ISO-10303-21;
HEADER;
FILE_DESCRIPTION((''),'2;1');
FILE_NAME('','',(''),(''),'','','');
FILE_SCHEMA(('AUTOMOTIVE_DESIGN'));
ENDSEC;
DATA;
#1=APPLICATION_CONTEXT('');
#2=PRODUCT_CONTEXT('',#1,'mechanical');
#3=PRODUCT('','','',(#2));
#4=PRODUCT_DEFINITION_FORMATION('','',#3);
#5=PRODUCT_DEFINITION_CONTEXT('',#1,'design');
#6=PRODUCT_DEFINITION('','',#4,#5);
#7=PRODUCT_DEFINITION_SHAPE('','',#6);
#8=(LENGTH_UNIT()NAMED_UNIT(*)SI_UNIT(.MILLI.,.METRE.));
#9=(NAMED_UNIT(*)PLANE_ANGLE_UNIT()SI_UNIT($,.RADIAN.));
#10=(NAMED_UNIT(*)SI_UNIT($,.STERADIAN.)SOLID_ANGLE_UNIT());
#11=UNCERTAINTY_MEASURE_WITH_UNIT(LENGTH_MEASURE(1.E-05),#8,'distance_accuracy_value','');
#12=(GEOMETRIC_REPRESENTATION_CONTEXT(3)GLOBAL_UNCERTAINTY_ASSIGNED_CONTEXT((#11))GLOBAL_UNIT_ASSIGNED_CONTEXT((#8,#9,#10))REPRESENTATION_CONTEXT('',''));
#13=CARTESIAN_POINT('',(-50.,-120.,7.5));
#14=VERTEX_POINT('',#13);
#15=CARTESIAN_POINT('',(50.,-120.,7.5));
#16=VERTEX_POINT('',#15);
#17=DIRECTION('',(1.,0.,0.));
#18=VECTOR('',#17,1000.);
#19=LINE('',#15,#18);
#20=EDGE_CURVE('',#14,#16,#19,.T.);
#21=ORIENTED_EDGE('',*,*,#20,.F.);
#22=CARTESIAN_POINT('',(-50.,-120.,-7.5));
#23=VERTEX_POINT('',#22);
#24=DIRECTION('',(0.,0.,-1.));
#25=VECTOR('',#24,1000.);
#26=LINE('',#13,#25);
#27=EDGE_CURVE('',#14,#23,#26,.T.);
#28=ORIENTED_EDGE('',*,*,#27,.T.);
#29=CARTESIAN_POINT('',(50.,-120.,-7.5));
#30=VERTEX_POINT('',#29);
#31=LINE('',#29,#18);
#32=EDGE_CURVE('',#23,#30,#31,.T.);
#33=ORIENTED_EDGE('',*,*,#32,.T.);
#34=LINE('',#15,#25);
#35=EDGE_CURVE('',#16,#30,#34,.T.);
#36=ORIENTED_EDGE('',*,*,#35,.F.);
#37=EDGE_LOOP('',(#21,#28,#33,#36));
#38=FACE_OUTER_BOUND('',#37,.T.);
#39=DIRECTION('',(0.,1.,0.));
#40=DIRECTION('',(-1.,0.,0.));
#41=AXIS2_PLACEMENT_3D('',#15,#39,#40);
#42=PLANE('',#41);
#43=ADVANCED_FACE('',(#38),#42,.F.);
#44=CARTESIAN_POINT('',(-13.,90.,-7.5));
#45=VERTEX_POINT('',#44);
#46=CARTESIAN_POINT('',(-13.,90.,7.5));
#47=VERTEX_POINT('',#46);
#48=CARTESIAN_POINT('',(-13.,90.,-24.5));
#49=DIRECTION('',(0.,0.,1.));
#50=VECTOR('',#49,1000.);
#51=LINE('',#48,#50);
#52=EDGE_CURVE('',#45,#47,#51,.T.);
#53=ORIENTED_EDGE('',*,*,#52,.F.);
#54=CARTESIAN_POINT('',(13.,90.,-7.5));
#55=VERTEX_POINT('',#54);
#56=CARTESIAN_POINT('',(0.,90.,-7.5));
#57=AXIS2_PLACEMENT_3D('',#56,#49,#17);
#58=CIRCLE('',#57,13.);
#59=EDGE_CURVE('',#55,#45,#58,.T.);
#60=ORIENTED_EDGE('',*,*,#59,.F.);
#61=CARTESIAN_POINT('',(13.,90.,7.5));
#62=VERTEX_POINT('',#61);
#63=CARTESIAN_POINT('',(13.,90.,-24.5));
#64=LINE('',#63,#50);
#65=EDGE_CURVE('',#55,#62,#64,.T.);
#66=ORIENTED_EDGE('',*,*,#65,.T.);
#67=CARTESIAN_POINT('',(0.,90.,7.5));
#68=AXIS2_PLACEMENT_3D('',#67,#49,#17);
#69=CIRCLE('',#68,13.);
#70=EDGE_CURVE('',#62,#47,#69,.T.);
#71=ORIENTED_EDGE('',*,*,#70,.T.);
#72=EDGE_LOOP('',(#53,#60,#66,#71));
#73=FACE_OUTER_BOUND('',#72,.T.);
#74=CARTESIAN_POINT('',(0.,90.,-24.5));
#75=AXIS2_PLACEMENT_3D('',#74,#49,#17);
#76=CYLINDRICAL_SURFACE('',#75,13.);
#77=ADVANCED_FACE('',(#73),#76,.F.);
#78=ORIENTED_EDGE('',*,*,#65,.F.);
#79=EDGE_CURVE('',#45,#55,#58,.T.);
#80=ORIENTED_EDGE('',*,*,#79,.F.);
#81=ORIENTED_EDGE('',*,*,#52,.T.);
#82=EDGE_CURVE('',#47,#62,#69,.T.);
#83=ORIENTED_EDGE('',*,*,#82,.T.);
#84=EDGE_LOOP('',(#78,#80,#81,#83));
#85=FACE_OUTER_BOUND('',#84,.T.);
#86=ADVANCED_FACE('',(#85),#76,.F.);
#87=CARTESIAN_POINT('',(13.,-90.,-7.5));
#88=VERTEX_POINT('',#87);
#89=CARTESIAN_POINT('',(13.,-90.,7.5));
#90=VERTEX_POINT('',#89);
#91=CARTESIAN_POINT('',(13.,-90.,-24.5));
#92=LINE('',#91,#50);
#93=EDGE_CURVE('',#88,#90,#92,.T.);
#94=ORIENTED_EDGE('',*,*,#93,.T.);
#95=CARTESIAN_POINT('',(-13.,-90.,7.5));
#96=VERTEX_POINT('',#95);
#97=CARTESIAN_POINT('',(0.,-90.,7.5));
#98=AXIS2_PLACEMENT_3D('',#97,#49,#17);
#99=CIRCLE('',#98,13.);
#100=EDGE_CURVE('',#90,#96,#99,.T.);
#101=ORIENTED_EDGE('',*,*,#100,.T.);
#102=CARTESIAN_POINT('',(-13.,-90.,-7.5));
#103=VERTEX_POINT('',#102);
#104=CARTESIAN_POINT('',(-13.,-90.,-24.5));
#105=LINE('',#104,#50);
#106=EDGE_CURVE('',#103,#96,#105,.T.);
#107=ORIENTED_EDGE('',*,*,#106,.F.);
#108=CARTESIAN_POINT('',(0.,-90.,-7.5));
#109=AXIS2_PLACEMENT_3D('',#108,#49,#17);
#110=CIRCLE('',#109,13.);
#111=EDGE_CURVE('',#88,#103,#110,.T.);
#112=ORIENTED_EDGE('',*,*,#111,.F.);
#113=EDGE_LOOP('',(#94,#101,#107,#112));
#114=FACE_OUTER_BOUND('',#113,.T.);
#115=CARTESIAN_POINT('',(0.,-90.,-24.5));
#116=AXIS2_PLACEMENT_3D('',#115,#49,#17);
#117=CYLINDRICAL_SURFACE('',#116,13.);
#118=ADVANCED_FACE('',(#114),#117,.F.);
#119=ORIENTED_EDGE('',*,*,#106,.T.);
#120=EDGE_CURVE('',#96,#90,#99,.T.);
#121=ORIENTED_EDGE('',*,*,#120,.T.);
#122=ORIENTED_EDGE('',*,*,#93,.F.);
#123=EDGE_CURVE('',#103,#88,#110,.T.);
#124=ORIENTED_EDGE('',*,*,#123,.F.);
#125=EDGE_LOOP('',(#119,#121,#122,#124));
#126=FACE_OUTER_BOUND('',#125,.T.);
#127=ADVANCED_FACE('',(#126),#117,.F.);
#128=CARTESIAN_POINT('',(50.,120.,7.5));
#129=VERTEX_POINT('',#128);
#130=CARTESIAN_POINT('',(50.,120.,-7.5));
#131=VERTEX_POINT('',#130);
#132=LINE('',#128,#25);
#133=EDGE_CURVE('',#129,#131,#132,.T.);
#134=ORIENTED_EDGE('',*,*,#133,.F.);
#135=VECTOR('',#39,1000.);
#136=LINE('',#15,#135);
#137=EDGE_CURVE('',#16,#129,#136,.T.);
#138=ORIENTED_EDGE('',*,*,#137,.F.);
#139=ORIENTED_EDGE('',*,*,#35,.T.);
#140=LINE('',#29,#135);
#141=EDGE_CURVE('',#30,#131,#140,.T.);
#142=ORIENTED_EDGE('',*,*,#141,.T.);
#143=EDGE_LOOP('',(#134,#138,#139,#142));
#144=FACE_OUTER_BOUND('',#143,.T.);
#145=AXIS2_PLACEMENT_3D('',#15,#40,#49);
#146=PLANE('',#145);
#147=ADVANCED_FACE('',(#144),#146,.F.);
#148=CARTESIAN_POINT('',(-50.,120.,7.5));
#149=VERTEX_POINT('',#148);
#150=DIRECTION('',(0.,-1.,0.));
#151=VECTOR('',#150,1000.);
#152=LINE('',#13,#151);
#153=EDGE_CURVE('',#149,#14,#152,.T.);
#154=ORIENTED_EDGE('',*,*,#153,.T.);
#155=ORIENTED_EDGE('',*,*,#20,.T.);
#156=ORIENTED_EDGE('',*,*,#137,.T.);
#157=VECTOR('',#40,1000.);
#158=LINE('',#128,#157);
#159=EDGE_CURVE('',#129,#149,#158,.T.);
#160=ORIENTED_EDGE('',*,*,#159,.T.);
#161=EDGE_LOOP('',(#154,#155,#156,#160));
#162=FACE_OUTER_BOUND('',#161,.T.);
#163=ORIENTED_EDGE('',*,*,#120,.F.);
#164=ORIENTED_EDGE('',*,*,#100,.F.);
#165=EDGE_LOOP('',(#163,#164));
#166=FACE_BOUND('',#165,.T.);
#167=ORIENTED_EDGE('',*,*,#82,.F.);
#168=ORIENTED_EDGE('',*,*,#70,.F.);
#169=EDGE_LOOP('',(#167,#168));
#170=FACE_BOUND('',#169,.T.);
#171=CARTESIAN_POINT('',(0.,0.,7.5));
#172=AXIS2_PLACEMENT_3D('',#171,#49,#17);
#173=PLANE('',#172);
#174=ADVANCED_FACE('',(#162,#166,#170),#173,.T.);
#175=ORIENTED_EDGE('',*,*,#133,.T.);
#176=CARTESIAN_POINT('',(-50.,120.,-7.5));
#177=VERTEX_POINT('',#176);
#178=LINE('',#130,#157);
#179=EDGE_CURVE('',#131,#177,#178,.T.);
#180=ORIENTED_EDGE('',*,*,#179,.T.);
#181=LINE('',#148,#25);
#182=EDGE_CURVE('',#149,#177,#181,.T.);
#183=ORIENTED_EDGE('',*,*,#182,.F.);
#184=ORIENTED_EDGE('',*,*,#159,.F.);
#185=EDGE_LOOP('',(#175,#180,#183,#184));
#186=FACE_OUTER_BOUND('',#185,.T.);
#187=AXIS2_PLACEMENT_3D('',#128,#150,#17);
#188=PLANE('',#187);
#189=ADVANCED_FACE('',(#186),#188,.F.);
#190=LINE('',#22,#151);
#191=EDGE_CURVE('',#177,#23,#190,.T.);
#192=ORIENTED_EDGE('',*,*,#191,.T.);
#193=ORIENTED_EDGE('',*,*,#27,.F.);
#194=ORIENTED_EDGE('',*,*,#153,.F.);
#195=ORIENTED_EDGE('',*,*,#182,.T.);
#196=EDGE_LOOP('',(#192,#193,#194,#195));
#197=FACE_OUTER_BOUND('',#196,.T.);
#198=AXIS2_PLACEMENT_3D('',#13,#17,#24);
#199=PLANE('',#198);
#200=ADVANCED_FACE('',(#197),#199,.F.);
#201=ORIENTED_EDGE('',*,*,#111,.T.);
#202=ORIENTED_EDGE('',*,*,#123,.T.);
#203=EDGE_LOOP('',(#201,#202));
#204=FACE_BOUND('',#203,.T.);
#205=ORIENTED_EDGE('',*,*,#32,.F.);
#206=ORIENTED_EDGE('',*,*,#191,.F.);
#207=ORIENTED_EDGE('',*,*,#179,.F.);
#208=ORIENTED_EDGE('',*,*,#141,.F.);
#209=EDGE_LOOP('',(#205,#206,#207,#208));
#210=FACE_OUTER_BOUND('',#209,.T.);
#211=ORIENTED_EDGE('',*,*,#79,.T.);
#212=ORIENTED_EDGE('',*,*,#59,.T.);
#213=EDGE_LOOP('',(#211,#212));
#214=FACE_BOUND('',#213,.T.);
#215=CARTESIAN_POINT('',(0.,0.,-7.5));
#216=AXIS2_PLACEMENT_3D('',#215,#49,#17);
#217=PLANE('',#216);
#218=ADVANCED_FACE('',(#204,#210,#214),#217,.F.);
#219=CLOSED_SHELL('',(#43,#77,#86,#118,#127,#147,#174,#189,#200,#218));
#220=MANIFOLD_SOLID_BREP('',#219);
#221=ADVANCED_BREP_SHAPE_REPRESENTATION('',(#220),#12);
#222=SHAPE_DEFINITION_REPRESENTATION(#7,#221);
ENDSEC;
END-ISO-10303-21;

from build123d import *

# Parameters (mm, degrees)
SKETCH1_W           = 100
SKETCH1_H           = 240
BOSS_EXTRUDE1_DEPTH = 7.5
SKETCH2_R           = 13
CUT_EXTRUDE1_DEPTH  = 32


with BuildPart() as part:
    # Sketch1 → Boss-Extrude1 (new, symmetric)
    with BuildSketch(Plane.XY):
        Rectangle(SKETCH1_W, SKETCH1_H)
    extrude(amount=BOSS_EXTRUDE1_DEPTH, both=True)

    # Sketch2 → Cut-Extrude1 (cut)
    with BuildSketch(Plane.XY.offset(7.5)):
        with Locations((0, 90)):
            Circle(SKETCH2_R)
        with Locations((0, -90)):
            Circle(SKETCH2_R)
    extrude(amount=-CUT_EXTRUDE1_DEPTH, mode=Mode.SUBTRACT)


solid = part.part
